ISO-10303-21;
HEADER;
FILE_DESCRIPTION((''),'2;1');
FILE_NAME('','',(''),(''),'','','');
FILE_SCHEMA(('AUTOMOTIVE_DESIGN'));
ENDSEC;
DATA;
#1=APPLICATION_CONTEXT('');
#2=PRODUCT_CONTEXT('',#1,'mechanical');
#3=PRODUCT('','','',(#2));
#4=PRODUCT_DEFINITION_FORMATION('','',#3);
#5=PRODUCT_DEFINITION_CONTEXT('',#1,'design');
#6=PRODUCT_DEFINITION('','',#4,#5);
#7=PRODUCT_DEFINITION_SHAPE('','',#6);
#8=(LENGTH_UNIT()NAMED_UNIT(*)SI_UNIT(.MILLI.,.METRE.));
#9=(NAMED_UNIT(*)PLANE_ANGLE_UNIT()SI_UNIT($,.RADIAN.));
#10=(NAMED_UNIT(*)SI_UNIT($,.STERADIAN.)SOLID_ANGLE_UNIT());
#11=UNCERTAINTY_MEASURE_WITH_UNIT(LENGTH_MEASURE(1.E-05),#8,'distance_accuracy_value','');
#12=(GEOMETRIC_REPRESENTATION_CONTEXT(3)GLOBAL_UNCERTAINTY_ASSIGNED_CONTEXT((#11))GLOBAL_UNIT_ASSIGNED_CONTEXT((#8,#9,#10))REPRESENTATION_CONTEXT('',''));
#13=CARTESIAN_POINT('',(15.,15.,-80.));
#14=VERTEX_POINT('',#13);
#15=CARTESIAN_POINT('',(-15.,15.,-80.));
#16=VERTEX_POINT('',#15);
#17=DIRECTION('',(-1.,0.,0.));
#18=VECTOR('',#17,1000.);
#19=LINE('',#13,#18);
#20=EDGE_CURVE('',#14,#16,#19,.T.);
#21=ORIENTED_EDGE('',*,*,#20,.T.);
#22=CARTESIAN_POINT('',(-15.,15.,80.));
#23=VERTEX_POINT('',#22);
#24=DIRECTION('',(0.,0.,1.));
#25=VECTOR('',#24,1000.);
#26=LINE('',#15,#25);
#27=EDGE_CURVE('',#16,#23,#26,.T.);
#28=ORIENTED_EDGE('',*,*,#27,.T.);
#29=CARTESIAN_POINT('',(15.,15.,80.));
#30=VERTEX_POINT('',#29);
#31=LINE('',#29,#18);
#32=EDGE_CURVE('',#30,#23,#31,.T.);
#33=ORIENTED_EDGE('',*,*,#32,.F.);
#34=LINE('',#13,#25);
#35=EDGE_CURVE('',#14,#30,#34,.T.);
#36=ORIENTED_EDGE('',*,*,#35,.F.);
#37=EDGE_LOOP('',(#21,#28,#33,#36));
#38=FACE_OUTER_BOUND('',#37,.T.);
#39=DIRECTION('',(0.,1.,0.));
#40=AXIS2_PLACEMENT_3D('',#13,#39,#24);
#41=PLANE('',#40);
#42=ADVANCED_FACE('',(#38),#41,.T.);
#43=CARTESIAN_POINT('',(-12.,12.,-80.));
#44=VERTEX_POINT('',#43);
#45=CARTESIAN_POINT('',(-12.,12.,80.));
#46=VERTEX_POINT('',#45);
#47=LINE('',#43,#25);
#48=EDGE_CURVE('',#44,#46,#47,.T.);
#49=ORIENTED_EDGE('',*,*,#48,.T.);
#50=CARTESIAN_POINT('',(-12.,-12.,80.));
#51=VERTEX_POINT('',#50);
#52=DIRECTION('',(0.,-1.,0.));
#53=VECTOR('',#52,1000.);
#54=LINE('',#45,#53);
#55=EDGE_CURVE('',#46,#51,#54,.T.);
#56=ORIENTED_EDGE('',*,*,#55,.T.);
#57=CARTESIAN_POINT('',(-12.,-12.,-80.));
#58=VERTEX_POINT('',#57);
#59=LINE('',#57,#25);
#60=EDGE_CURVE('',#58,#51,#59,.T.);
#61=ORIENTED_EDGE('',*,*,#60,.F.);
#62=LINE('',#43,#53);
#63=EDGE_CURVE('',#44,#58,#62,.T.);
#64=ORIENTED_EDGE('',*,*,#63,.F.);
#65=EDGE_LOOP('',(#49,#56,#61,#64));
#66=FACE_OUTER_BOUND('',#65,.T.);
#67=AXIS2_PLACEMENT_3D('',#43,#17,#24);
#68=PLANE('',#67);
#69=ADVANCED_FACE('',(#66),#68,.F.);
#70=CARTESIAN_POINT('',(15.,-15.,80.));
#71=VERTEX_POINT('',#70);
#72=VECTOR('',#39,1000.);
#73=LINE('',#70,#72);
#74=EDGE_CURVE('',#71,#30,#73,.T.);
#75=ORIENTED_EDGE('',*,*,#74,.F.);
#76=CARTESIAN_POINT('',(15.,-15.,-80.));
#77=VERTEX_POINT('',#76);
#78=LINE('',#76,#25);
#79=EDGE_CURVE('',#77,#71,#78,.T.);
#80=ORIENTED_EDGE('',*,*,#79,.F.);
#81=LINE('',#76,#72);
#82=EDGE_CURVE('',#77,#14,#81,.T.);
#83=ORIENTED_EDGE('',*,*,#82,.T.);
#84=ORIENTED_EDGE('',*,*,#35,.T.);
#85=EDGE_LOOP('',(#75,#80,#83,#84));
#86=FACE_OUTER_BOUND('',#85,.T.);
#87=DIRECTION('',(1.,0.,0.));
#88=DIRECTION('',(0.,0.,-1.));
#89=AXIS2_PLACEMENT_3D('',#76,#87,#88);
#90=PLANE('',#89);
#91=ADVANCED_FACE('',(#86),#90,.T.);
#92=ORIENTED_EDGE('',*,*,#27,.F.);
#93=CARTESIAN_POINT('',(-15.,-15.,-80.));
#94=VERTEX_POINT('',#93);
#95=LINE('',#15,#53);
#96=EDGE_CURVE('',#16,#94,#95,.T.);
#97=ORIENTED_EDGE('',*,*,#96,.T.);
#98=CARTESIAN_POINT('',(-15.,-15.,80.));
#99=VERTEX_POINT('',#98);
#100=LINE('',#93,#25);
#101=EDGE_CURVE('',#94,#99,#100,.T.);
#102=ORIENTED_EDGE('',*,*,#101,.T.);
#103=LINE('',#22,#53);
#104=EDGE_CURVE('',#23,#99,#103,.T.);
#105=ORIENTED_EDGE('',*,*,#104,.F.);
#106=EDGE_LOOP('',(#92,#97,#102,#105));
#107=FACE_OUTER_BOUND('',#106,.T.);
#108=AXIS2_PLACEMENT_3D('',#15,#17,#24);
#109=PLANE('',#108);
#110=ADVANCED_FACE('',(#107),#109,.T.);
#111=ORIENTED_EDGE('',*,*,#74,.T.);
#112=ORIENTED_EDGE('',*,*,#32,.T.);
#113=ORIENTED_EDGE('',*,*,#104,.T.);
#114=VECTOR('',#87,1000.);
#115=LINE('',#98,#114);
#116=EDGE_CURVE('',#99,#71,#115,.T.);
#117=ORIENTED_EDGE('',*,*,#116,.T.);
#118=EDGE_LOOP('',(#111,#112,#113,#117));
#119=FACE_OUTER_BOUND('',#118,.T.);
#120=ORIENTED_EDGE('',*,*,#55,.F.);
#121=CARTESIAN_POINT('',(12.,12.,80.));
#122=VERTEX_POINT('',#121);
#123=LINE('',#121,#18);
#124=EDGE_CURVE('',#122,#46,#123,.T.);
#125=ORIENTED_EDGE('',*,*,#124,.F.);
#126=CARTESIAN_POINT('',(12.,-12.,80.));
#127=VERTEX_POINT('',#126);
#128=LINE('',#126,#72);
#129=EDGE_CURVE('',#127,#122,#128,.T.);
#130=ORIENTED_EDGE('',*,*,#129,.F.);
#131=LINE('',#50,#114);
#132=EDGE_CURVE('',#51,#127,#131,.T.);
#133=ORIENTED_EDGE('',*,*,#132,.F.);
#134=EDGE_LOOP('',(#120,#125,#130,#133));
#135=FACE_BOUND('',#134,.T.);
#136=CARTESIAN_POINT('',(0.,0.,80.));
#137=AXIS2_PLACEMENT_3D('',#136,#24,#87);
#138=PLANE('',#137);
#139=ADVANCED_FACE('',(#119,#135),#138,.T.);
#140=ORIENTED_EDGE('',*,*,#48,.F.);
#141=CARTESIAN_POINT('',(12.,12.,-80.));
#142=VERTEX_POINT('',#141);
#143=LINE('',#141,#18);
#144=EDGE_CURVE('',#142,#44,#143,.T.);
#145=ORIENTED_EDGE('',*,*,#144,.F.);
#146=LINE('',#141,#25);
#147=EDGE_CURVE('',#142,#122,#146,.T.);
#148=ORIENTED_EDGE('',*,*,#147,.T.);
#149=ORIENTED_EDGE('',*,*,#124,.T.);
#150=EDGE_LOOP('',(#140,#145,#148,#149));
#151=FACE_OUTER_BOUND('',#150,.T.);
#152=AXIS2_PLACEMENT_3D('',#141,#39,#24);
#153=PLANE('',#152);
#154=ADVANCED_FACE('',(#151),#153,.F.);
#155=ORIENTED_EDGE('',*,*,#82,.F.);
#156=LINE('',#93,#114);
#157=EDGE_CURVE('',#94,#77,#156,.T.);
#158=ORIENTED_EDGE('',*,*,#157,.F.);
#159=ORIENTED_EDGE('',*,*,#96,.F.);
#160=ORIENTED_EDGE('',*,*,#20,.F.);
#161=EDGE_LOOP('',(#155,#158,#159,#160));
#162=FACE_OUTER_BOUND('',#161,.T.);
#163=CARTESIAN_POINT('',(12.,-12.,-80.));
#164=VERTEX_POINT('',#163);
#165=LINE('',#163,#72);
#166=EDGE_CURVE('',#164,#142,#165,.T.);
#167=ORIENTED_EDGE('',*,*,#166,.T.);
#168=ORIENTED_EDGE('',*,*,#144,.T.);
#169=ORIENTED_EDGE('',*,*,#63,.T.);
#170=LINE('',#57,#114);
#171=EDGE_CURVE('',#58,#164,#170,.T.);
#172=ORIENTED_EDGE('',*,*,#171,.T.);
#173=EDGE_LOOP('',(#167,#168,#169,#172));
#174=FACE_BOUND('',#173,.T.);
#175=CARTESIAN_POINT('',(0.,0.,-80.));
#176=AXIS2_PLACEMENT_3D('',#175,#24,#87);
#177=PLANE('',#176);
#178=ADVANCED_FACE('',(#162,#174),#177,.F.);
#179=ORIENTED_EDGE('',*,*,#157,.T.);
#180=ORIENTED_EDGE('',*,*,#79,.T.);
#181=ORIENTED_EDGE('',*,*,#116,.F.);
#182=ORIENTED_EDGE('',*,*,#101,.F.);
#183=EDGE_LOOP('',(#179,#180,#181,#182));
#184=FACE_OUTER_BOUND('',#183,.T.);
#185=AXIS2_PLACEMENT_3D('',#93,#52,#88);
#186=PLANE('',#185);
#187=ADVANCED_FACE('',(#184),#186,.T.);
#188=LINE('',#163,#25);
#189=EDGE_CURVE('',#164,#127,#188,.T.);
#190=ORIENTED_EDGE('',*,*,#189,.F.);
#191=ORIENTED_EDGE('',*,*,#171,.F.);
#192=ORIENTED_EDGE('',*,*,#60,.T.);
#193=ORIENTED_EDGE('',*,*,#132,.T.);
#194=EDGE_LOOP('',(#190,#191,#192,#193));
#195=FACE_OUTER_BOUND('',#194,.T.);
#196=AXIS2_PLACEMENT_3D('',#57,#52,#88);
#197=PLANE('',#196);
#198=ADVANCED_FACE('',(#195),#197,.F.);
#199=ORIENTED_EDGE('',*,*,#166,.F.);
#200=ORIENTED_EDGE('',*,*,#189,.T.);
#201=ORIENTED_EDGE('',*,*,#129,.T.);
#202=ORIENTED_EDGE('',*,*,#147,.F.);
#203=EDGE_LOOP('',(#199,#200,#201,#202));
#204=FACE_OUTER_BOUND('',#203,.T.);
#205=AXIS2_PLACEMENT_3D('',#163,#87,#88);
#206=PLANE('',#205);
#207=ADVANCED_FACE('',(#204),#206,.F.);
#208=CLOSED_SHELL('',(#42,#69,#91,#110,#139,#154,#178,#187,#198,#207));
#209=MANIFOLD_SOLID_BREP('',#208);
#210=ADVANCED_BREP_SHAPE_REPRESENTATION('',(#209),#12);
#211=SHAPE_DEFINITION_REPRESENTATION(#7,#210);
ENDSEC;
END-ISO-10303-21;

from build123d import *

# Parameters (mm, degrees)
SKETCH_1_W      = 30
SKETCH_1_H      = 30
SKETCH_1_W_2    = 24
SKETCH_1_H_2    = 24
EXTRUDE_1_DEPTH = 80


with BuildPart() as part:
    # 草图1 → 凸台-拉伸1 (new, symmetric)
    with BuildSketch(Plane.XY):
        Rectangle(SKETCH_1_W, SKETCH_1_H)
        Rectangle(SKETCH_1_W_2, SKETCH_1_H_2, mode=Mode.SUBTRACT)
    extrude(amount=EXTRUDE_1_DEPTH, both=True)


solid = part.part
